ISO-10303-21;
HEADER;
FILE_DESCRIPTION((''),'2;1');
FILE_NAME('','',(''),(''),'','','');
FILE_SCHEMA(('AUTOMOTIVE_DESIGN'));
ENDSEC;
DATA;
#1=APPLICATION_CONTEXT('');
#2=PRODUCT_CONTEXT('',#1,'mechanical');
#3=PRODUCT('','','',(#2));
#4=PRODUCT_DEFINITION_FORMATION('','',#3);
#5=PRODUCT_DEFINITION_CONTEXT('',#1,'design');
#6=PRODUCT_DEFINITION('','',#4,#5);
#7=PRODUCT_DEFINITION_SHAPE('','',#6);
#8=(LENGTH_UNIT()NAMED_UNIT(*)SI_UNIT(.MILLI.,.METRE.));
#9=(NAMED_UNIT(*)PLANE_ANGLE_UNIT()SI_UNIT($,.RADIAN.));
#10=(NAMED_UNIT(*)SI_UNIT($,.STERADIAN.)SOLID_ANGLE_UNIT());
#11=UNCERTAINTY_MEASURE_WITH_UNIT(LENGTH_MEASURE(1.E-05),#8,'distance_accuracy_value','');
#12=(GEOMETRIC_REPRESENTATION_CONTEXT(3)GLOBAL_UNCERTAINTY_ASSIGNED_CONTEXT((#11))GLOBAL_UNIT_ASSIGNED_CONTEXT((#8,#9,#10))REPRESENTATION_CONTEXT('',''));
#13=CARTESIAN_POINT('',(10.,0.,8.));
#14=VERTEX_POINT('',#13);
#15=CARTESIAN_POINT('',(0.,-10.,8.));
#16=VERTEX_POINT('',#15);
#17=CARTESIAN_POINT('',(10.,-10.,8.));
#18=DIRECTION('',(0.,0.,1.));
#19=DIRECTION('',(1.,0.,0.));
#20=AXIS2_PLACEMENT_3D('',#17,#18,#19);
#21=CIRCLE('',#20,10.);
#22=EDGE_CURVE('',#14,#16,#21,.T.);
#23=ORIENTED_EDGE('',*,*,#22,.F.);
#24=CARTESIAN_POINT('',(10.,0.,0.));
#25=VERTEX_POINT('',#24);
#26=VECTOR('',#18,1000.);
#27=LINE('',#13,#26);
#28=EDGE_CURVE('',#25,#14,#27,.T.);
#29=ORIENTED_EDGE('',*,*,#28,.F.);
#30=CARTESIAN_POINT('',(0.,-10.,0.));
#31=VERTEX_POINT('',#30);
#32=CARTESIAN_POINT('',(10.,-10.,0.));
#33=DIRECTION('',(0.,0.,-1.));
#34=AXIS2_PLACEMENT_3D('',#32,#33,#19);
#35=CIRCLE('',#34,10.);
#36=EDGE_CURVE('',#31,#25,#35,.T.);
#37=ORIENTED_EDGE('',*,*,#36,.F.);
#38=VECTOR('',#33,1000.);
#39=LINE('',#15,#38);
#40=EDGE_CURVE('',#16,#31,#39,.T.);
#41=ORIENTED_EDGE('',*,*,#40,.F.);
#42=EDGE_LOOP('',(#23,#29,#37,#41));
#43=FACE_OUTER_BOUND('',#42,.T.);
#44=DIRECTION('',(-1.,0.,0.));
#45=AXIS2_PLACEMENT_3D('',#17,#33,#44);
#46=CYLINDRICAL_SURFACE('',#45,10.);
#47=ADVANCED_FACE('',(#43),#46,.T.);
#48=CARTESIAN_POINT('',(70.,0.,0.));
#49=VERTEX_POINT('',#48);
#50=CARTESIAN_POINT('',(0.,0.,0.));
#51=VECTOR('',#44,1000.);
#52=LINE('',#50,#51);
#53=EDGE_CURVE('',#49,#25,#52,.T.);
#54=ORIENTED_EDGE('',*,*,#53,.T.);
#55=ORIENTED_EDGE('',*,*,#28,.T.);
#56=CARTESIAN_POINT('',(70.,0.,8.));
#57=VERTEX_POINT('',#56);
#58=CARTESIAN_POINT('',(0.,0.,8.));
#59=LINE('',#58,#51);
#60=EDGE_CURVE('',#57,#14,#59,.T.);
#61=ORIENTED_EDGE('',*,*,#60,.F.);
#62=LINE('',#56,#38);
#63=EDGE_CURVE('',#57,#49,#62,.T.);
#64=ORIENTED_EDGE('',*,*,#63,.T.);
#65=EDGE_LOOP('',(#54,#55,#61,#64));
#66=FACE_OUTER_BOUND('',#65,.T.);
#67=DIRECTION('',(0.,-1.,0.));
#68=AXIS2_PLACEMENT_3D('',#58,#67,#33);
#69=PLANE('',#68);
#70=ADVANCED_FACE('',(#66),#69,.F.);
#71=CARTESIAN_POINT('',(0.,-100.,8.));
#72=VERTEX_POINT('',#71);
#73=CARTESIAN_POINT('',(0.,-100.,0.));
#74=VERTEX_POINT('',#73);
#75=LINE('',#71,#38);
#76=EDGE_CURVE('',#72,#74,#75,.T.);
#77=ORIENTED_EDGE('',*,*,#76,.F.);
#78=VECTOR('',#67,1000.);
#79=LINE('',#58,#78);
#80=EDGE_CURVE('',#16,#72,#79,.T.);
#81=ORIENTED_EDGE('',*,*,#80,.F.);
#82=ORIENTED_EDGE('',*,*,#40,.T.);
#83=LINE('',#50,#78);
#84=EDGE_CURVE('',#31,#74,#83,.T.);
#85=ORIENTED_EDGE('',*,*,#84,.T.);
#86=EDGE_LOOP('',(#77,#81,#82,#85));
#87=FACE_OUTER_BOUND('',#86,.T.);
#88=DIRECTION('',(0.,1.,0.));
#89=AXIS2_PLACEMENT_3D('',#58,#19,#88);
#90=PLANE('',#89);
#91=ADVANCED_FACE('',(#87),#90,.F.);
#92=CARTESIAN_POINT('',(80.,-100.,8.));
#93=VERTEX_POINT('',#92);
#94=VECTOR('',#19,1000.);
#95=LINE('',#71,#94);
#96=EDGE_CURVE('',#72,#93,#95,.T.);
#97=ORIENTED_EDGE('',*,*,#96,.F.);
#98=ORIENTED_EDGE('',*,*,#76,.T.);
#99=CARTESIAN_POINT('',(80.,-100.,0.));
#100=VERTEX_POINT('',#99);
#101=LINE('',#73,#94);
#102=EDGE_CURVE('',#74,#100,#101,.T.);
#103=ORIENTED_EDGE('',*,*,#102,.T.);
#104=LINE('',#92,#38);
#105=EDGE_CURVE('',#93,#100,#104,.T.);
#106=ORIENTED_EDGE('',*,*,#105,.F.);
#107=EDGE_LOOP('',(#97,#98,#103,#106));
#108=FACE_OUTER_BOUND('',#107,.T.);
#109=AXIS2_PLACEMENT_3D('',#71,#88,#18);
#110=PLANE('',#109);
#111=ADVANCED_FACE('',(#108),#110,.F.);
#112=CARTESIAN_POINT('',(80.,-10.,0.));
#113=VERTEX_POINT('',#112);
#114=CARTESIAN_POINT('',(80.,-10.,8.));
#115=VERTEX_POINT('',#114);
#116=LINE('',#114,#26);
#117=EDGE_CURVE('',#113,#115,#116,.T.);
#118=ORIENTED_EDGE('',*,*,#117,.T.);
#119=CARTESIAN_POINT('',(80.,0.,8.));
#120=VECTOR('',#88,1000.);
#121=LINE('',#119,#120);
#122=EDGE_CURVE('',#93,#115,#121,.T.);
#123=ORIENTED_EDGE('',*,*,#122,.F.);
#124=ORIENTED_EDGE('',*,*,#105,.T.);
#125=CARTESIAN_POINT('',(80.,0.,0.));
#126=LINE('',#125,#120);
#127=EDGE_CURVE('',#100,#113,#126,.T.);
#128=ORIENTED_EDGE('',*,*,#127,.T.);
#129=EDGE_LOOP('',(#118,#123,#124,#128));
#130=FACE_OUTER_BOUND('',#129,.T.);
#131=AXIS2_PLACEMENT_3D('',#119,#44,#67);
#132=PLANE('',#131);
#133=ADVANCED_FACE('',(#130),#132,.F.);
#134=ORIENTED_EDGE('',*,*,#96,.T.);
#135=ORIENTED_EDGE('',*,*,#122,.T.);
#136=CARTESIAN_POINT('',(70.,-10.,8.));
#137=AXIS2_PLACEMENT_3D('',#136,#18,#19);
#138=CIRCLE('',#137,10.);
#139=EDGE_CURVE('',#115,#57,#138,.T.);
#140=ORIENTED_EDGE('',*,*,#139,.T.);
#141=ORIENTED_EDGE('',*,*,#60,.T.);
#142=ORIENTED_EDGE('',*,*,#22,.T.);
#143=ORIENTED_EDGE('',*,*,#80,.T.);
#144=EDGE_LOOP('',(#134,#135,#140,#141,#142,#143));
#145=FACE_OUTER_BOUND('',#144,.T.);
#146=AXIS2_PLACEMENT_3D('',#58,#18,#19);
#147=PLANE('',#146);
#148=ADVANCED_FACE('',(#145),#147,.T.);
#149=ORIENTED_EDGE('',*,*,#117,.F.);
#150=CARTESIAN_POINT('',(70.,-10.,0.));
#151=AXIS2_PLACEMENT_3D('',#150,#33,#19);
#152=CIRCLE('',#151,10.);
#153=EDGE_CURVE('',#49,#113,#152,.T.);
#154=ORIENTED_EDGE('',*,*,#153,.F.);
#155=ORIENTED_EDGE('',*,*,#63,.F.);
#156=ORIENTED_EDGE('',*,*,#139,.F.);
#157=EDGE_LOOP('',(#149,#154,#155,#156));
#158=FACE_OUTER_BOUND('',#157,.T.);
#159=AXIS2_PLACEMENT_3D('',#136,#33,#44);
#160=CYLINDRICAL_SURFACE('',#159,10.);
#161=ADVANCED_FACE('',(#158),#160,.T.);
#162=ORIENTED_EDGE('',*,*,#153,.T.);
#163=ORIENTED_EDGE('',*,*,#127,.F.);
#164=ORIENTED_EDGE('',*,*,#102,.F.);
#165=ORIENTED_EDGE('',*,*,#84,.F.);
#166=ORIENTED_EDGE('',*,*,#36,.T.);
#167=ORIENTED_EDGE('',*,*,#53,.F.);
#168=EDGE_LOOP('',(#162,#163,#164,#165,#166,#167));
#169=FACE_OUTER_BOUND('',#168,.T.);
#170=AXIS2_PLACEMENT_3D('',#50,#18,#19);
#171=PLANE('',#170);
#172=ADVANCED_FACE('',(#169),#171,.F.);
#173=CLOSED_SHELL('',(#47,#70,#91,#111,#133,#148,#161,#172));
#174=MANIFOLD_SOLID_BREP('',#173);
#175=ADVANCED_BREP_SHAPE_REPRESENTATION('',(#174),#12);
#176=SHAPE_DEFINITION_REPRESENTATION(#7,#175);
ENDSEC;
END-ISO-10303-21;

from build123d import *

# Parameters (mm, degrees)
SKETCH1_W           = 80
SKETCH1_H           = 100
BOSS_EXTRUDE1_DEPTH = 8
FILLET1_R           = 10


with BuildPart() as part:
    # Sketch1 → Boss-Extrude1 (new body)
    with BuildSketch(Plane.XY):
        with Locations((40, -50)):
            Rectangle(SKETCH1_W, SKETCH1_H)
    extrude(amount=BOSS_EXTRUDE1_DEPTH)

    # Fillet1
    fillet1_edges = [part.edges().sort_by_distance(p)[0] for p in [
        (0, 0, 4),
        (80, 0, 4),
    ]]
    fillet(fillet1_edges, radius=FILLET1_R)


solid = part.part
